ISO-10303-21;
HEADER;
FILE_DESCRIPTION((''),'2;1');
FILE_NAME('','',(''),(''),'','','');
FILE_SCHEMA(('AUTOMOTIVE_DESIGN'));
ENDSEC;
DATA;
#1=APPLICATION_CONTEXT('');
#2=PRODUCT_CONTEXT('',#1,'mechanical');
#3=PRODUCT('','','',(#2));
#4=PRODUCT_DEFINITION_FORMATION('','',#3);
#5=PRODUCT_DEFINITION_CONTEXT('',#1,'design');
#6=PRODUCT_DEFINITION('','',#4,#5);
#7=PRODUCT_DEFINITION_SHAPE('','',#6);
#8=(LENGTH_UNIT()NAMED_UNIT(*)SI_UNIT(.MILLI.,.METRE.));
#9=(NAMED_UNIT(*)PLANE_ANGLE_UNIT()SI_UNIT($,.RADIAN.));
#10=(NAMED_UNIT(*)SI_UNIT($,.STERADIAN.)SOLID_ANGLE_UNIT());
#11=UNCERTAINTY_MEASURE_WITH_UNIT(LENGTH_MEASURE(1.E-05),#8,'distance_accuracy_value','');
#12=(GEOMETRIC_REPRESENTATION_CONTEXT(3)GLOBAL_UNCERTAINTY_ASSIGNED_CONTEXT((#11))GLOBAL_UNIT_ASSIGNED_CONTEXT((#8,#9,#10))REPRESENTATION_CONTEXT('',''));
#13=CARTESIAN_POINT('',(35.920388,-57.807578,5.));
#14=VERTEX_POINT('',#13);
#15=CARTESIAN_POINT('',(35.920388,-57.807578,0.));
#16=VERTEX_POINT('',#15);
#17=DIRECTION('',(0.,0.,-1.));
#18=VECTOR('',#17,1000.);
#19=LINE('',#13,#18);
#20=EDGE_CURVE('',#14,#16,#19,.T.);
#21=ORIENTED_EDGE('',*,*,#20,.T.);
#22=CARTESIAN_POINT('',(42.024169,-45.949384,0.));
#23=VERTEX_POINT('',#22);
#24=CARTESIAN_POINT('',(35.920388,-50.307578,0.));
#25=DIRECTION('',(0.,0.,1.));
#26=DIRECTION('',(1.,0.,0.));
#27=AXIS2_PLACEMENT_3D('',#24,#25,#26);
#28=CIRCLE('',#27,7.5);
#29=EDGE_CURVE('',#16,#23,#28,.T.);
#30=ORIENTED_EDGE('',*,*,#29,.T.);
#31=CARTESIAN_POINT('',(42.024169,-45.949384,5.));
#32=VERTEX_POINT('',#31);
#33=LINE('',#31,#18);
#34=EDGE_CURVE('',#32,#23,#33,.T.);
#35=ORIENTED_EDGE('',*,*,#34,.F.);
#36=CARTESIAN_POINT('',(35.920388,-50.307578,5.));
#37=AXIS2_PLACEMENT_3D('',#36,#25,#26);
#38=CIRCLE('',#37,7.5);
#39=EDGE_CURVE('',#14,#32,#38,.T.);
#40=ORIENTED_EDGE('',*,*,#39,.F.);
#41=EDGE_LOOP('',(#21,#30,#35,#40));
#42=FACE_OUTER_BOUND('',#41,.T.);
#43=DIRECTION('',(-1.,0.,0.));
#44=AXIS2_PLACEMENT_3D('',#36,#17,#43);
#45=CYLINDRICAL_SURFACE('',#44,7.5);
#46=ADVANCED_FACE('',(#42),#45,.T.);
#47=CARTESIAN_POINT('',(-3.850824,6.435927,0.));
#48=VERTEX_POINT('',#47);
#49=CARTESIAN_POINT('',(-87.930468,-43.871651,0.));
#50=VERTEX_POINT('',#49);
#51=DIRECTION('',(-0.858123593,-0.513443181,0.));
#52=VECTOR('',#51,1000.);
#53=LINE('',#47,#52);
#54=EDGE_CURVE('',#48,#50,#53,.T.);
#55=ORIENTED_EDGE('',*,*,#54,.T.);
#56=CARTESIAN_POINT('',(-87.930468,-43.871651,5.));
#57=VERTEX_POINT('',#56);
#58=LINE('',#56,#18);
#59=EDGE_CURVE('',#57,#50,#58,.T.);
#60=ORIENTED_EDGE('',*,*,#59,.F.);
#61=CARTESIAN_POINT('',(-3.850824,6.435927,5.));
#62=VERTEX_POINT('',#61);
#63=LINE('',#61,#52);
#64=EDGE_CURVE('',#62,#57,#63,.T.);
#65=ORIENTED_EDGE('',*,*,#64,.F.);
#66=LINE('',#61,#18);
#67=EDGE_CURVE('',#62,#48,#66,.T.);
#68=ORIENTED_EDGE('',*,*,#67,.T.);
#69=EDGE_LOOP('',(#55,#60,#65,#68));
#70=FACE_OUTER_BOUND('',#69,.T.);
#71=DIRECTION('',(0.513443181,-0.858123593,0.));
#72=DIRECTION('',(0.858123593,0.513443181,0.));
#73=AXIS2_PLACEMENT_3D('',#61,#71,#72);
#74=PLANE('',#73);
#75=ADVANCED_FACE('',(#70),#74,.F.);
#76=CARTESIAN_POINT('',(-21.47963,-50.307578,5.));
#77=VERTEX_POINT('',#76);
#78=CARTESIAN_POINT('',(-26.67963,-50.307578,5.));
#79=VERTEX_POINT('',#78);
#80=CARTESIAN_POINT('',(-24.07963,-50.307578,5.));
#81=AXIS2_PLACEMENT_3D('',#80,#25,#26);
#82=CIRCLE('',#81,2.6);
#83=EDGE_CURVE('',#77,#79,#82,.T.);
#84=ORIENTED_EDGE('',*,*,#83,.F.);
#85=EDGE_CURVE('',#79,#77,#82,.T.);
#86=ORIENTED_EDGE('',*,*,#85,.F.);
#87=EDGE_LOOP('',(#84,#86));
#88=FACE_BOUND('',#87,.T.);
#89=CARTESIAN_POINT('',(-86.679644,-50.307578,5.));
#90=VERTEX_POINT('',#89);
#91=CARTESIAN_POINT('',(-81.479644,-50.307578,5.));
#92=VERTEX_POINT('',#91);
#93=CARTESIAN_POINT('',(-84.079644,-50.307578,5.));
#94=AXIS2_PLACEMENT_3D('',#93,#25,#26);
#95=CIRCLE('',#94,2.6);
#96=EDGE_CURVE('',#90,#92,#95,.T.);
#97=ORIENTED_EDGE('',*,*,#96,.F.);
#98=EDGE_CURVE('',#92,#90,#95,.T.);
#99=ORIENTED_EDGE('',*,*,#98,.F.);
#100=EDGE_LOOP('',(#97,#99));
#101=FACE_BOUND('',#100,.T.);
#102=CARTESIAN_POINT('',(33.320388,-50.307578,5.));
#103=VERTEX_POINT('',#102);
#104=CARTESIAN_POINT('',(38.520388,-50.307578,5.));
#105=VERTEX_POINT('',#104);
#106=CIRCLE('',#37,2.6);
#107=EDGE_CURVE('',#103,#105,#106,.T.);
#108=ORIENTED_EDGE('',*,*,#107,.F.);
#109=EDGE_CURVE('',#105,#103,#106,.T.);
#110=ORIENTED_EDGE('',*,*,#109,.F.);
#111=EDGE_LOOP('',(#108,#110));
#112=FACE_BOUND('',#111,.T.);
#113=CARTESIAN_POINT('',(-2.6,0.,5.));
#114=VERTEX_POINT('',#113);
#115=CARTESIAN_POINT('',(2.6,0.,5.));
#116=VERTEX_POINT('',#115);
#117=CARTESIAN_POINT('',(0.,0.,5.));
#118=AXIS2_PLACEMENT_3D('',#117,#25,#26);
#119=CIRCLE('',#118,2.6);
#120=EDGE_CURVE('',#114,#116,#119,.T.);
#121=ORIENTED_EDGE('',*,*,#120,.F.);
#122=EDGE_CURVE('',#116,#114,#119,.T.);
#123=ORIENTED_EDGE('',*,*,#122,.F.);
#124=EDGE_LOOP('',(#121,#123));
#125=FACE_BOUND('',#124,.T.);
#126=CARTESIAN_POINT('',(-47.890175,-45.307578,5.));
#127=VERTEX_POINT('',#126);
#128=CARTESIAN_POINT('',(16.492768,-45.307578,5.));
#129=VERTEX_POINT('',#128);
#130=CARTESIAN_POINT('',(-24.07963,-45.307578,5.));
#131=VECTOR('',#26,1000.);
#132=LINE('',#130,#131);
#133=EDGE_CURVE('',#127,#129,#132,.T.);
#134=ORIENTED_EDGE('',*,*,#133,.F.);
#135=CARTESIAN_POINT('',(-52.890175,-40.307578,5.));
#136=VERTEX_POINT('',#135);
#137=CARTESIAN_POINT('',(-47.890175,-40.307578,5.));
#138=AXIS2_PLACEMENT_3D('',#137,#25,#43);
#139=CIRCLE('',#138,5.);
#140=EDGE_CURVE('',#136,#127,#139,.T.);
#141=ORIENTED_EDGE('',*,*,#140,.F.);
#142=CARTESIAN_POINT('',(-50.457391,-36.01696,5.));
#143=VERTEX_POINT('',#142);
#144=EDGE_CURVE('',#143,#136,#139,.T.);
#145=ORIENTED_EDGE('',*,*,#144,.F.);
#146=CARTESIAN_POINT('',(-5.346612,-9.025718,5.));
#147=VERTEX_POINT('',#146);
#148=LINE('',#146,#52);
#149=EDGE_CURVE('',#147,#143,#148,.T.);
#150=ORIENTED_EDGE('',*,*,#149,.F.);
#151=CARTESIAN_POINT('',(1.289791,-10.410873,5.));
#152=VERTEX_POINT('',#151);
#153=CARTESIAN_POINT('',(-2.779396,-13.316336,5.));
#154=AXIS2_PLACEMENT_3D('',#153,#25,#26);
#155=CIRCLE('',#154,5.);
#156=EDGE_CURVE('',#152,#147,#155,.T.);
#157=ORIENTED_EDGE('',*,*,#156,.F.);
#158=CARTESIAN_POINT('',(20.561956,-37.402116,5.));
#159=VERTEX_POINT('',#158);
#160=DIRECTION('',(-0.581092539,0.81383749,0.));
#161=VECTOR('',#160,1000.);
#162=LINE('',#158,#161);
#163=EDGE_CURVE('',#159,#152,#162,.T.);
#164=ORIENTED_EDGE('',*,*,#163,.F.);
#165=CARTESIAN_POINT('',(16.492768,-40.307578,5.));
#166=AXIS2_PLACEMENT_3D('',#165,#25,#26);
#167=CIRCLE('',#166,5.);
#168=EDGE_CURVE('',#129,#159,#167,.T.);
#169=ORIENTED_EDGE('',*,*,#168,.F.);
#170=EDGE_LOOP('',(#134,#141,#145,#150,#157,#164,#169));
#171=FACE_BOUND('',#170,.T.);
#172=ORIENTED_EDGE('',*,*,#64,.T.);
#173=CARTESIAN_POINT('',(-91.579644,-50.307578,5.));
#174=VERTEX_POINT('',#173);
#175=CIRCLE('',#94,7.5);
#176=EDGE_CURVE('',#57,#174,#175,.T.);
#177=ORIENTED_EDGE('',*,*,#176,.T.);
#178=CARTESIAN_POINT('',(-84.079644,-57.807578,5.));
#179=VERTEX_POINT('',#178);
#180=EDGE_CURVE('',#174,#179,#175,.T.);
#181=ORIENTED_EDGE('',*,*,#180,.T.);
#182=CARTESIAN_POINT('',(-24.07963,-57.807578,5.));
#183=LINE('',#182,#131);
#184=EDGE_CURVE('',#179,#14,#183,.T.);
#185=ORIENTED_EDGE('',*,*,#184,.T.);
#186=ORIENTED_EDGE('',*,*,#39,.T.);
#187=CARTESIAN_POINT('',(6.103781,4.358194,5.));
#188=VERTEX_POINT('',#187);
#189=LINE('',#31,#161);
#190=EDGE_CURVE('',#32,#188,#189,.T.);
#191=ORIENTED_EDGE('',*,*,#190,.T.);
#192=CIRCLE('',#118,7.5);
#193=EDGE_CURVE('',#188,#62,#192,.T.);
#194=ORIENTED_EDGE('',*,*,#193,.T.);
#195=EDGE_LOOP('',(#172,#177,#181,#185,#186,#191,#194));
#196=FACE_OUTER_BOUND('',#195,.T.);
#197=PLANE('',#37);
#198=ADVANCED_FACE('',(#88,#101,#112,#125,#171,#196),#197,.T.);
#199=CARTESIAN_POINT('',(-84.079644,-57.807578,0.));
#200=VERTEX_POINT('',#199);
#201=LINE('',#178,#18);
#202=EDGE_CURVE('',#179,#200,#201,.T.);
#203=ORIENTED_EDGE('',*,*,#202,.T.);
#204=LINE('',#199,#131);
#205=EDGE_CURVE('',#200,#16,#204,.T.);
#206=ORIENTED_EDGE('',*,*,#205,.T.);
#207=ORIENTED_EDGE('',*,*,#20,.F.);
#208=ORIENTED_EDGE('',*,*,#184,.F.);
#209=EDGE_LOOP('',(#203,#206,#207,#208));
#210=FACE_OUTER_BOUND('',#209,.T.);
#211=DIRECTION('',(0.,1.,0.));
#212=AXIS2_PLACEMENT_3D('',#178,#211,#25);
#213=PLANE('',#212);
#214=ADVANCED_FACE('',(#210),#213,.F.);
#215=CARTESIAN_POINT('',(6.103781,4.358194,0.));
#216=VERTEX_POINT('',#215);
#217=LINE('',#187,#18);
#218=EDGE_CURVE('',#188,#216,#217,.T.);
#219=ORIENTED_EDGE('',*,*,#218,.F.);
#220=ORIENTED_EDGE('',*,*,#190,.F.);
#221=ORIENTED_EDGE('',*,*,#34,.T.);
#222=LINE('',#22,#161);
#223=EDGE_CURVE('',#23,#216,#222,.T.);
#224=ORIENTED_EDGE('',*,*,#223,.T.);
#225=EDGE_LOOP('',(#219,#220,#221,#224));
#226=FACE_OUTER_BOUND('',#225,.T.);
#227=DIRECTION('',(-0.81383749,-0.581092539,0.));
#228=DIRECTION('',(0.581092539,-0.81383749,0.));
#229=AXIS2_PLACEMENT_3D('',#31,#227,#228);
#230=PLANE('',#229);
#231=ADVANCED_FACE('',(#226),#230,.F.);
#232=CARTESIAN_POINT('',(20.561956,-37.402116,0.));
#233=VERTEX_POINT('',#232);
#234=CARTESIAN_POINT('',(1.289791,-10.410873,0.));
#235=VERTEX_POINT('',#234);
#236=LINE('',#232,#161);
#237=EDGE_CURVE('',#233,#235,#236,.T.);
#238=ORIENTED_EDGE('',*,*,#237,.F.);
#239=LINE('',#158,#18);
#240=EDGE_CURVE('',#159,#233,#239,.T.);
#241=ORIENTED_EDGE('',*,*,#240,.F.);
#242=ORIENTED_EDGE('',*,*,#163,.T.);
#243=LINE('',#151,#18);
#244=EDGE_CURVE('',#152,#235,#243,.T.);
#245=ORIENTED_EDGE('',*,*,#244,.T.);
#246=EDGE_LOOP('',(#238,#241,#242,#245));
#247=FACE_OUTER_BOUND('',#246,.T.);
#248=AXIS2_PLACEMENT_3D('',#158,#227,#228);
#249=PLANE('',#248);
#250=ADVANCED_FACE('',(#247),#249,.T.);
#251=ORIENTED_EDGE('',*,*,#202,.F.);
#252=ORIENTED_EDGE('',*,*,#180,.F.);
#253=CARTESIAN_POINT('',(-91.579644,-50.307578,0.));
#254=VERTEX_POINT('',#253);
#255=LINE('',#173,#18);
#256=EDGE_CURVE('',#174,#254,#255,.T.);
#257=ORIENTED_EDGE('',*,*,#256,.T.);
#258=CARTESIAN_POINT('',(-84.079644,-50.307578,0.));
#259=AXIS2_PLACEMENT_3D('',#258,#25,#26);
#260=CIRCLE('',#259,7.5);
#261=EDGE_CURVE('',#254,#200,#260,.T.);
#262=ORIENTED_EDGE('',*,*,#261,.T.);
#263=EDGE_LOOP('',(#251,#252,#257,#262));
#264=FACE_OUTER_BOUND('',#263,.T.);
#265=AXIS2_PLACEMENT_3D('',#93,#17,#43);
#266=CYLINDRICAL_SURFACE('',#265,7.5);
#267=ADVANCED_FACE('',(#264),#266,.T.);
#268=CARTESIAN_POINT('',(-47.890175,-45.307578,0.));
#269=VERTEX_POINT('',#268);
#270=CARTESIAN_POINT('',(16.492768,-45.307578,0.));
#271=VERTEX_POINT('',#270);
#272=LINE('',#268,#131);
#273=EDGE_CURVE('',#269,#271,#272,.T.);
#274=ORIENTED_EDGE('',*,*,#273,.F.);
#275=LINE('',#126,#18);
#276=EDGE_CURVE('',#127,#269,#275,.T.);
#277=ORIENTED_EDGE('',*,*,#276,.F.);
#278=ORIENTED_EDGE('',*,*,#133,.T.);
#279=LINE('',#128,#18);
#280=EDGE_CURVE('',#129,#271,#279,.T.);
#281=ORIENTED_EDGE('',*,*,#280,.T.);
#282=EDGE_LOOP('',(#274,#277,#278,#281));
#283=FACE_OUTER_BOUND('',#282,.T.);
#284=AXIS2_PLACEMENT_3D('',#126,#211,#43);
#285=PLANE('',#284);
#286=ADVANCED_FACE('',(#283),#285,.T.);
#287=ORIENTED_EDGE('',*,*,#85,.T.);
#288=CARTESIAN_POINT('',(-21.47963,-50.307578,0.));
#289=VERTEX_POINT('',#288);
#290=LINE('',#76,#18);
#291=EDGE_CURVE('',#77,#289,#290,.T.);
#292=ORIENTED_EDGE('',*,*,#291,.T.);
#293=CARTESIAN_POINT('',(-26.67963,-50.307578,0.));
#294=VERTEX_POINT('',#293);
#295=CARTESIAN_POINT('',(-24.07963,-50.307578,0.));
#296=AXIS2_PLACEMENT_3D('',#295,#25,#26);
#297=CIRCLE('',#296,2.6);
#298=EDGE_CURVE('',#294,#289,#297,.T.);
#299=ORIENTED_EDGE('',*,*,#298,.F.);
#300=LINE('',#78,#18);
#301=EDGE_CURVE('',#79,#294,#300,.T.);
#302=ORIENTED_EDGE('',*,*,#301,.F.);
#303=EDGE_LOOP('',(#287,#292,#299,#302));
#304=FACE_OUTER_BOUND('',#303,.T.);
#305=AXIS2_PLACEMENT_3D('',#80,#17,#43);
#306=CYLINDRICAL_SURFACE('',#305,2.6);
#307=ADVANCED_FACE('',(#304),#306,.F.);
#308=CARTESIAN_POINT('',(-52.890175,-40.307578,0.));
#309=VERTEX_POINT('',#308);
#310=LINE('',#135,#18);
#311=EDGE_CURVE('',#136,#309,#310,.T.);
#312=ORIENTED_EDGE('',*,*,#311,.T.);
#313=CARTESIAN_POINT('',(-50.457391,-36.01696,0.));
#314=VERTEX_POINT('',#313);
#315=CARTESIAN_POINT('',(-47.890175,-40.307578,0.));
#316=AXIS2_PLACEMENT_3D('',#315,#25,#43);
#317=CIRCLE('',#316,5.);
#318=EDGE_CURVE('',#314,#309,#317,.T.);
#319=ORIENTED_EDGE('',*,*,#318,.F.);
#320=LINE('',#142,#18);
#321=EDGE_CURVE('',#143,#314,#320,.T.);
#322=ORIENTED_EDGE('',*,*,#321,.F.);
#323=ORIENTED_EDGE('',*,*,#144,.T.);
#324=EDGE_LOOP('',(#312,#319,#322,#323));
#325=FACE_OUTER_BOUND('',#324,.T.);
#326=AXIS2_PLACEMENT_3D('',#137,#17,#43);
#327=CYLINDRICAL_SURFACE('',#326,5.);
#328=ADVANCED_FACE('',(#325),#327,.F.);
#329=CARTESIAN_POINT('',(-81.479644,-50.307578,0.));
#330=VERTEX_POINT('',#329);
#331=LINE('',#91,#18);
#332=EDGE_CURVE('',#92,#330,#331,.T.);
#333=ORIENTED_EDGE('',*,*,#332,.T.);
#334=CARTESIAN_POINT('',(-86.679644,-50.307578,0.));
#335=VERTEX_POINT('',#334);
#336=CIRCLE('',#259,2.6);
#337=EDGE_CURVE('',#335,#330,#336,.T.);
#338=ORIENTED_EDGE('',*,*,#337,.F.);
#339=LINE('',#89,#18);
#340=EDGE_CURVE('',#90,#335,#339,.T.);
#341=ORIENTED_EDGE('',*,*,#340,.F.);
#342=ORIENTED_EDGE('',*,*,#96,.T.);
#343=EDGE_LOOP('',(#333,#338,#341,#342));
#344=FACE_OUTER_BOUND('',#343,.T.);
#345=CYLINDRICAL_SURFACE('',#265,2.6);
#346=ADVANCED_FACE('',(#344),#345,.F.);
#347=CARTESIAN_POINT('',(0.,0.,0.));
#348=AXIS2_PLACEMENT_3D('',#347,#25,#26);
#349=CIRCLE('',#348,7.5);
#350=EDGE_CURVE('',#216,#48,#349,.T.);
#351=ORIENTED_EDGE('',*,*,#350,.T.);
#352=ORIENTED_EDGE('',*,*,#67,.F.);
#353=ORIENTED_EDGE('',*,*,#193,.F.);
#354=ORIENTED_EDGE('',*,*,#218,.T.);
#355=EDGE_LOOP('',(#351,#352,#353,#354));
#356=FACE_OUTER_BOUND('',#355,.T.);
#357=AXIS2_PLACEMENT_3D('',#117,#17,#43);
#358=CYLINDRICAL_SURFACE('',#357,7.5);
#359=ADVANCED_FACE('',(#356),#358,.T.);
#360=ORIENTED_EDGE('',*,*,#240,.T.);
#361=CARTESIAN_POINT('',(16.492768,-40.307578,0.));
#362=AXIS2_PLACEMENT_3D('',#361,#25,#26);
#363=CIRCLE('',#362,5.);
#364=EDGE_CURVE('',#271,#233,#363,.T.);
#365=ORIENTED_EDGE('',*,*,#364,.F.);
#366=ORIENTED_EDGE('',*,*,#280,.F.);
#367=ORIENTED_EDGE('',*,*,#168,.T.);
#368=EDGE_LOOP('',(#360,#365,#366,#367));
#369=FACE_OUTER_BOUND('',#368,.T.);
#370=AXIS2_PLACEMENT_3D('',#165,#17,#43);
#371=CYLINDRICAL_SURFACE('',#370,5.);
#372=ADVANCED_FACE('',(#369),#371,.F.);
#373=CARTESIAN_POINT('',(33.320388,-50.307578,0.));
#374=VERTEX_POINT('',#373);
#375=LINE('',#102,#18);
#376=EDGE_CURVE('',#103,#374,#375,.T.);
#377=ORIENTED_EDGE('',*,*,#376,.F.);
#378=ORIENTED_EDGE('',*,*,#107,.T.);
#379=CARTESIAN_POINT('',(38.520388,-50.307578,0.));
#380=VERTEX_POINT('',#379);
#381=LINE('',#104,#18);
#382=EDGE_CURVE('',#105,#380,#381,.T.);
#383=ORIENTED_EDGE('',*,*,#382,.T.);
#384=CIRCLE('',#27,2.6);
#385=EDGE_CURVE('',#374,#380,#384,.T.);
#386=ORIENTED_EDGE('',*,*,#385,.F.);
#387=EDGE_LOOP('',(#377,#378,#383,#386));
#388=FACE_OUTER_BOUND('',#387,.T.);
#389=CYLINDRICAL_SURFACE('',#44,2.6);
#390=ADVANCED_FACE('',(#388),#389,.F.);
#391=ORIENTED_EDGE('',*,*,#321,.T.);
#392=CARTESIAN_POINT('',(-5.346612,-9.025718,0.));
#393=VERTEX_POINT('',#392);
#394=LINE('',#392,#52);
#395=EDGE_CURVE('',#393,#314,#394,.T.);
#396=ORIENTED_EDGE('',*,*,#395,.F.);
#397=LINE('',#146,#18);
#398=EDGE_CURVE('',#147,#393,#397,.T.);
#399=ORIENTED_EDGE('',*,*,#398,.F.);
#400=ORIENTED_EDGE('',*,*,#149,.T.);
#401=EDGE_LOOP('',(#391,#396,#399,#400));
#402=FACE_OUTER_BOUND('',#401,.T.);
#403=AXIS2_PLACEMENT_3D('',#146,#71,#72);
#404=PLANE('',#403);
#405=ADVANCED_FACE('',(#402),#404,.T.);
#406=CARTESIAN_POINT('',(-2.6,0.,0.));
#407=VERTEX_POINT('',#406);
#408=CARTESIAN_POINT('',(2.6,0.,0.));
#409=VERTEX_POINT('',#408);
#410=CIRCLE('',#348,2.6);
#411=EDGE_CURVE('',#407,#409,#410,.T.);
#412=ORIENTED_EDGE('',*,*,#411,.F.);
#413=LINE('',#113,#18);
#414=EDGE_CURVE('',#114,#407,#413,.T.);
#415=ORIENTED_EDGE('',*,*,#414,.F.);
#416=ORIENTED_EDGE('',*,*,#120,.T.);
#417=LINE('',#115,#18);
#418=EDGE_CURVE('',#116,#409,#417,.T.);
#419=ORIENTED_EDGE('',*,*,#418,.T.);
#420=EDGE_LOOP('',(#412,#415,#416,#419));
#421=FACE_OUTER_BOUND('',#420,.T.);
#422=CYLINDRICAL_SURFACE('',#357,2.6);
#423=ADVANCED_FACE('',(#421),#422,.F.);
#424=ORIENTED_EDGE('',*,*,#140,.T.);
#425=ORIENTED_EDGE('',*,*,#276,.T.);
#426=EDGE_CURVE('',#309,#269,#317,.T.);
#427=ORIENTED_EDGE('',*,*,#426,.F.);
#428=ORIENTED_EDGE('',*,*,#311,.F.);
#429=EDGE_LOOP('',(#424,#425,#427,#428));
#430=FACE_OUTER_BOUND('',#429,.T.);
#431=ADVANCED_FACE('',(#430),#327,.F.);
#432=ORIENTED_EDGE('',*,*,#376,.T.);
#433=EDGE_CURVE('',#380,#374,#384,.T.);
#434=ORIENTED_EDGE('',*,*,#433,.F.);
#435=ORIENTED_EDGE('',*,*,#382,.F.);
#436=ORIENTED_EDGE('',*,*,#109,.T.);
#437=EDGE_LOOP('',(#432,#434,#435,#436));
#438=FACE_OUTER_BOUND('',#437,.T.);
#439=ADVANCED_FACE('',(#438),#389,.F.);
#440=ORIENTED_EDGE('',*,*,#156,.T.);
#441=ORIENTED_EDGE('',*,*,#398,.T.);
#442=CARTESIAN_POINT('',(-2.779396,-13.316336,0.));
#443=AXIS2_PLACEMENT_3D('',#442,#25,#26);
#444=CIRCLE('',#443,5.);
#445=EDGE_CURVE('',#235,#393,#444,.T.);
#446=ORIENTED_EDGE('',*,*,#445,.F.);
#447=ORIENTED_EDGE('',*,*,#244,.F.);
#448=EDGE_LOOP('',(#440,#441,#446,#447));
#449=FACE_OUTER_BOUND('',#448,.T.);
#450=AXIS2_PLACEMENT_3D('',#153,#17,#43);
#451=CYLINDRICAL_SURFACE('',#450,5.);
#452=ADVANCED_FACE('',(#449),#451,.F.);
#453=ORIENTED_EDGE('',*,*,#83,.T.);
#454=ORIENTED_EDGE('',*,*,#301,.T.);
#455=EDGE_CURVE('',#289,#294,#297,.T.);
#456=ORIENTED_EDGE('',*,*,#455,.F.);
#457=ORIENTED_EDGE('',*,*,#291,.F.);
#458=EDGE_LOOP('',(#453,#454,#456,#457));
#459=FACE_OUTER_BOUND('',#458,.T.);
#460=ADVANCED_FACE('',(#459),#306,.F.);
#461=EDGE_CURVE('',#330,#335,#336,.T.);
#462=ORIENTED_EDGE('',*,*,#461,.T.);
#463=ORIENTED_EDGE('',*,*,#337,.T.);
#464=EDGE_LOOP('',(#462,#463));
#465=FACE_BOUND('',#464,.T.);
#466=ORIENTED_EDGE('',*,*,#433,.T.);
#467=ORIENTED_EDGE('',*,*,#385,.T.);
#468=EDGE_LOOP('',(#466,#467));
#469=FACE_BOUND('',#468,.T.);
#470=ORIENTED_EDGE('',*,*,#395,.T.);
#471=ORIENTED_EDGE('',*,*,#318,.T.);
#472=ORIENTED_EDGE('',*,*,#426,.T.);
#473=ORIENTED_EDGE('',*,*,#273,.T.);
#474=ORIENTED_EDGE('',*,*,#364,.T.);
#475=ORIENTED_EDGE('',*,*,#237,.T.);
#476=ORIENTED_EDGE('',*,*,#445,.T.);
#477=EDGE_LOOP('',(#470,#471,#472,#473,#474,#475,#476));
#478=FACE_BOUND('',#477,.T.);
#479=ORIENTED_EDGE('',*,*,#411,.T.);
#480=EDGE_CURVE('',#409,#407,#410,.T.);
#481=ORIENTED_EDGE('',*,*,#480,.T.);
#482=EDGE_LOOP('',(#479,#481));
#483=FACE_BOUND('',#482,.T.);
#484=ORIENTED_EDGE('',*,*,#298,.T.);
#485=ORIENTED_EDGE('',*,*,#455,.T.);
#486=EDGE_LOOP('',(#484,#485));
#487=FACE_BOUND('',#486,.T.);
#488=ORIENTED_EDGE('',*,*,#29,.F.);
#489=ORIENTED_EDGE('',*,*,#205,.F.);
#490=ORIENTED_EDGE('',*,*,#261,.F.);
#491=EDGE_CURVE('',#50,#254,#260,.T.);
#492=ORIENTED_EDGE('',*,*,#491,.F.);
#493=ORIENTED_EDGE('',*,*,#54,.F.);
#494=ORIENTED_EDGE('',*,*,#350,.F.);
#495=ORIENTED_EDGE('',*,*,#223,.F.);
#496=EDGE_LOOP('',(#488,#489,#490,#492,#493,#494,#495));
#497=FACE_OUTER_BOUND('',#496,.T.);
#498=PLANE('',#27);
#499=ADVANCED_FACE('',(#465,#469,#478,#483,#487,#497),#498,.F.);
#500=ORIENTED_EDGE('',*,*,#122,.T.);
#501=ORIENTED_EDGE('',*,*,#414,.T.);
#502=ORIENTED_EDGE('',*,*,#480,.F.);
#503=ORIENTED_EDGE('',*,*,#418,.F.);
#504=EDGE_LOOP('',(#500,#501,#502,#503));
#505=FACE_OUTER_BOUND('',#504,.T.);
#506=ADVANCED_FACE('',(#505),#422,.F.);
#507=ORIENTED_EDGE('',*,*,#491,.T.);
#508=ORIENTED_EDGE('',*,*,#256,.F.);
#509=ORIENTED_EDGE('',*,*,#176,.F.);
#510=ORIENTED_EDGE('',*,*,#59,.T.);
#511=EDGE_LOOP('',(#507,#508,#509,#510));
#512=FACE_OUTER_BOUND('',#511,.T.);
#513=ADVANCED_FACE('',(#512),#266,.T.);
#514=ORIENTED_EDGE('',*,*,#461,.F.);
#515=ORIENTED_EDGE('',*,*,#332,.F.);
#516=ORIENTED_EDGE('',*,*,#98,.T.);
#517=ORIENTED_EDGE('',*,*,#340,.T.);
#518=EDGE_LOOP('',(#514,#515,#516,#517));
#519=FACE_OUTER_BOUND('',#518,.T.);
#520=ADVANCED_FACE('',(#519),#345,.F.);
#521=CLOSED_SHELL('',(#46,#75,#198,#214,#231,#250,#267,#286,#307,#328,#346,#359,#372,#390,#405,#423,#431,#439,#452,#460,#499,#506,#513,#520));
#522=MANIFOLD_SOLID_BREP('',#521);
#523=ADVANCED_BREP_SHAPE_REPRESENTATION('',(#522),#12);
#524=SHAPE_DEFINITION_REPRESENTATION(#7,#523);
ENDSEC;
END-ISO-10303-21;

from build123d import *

# Parameters (mm, degrees)
SKETCH1_R           = 2.6
BOSS_EXTRUDE1_DEPTH = 5


with BuildPart() as part:
    # Sketch1 → Boss-Extrude1 (new body)
    with BuildSketch(Plane.XY):
        with BuildLine():
            Line((42.024169285, -45.949384393), (6.103781177, 4.358194046))
            ThreePointArc((6.103781177, 4.358194046), (1.532383005, 7.341784683), (-3.850823854, 6.435926945))
            Line((-3.850823854, 6.435926945), (-87.930468078, -43.871651494))
            ThreePointArc((-87.930468078, -43.871651494), (-91.308733105, -52.305145448), (-84.079644224, -57.807578439))
            Line((-84.079644224, -57.807578439), (-24.079629528, -57.807578439))
            Line((-24.079629528, -57.807578439), (35.920388108, -57.807578439))
            ThreePointArc((35.920388108, -57.807578439), (42.588838278, -53.740037081), (42.024169285, -45.949384393))
        make_face()
        with Locations((-84.079644224, -50.307578439)):
            Circle(SKETCH1_R, mode=Mode.SUBTRACT)
        with Locations((-24.079629528, -50.307578439)):
            Circle(SKETCH1_R, mode=Mode.SUBTRACT)
        with Locations((35.920388108, -50.307578439)):
            Circle(SKETCH1_R, mode=Mode.SUBTRACT)
        Circle(SKETCH1_R, mode=Mode.SUBTRACT)
        with BuildLine():
            Line((-5.346611856, -9.025717813), (-50.457391397, -36.016960475))
            ThreePointArc((-50.457391397, -36.016960475), (-52.709568082, -41.639289778), (-47.890175494, -45.307578439))
            Line((-47.890175494, -45.307578439), (-24.079629528, -45.307578439))
            Line((-24.079629528, -45.307578439), (16.492768241, -45.307578439))
            ThreePointArc((16.492768241, -45.307578439), (20.938401688, -42.5958842), (20.561955693, -37.402115742))
            Line((20.561955693, -37.402115742), (1.289791498, -10.41087308))
            ThreePointArc((1.289791498, -10.41087308), (-1.757807283, -8.421812655), (-5.346611856, -9.025717813))
        make_face(mode=Mode.SUBTRACT)
    extrude(amount=BOSS_EXTRUDE1_DEPTH)


solid = part.part
